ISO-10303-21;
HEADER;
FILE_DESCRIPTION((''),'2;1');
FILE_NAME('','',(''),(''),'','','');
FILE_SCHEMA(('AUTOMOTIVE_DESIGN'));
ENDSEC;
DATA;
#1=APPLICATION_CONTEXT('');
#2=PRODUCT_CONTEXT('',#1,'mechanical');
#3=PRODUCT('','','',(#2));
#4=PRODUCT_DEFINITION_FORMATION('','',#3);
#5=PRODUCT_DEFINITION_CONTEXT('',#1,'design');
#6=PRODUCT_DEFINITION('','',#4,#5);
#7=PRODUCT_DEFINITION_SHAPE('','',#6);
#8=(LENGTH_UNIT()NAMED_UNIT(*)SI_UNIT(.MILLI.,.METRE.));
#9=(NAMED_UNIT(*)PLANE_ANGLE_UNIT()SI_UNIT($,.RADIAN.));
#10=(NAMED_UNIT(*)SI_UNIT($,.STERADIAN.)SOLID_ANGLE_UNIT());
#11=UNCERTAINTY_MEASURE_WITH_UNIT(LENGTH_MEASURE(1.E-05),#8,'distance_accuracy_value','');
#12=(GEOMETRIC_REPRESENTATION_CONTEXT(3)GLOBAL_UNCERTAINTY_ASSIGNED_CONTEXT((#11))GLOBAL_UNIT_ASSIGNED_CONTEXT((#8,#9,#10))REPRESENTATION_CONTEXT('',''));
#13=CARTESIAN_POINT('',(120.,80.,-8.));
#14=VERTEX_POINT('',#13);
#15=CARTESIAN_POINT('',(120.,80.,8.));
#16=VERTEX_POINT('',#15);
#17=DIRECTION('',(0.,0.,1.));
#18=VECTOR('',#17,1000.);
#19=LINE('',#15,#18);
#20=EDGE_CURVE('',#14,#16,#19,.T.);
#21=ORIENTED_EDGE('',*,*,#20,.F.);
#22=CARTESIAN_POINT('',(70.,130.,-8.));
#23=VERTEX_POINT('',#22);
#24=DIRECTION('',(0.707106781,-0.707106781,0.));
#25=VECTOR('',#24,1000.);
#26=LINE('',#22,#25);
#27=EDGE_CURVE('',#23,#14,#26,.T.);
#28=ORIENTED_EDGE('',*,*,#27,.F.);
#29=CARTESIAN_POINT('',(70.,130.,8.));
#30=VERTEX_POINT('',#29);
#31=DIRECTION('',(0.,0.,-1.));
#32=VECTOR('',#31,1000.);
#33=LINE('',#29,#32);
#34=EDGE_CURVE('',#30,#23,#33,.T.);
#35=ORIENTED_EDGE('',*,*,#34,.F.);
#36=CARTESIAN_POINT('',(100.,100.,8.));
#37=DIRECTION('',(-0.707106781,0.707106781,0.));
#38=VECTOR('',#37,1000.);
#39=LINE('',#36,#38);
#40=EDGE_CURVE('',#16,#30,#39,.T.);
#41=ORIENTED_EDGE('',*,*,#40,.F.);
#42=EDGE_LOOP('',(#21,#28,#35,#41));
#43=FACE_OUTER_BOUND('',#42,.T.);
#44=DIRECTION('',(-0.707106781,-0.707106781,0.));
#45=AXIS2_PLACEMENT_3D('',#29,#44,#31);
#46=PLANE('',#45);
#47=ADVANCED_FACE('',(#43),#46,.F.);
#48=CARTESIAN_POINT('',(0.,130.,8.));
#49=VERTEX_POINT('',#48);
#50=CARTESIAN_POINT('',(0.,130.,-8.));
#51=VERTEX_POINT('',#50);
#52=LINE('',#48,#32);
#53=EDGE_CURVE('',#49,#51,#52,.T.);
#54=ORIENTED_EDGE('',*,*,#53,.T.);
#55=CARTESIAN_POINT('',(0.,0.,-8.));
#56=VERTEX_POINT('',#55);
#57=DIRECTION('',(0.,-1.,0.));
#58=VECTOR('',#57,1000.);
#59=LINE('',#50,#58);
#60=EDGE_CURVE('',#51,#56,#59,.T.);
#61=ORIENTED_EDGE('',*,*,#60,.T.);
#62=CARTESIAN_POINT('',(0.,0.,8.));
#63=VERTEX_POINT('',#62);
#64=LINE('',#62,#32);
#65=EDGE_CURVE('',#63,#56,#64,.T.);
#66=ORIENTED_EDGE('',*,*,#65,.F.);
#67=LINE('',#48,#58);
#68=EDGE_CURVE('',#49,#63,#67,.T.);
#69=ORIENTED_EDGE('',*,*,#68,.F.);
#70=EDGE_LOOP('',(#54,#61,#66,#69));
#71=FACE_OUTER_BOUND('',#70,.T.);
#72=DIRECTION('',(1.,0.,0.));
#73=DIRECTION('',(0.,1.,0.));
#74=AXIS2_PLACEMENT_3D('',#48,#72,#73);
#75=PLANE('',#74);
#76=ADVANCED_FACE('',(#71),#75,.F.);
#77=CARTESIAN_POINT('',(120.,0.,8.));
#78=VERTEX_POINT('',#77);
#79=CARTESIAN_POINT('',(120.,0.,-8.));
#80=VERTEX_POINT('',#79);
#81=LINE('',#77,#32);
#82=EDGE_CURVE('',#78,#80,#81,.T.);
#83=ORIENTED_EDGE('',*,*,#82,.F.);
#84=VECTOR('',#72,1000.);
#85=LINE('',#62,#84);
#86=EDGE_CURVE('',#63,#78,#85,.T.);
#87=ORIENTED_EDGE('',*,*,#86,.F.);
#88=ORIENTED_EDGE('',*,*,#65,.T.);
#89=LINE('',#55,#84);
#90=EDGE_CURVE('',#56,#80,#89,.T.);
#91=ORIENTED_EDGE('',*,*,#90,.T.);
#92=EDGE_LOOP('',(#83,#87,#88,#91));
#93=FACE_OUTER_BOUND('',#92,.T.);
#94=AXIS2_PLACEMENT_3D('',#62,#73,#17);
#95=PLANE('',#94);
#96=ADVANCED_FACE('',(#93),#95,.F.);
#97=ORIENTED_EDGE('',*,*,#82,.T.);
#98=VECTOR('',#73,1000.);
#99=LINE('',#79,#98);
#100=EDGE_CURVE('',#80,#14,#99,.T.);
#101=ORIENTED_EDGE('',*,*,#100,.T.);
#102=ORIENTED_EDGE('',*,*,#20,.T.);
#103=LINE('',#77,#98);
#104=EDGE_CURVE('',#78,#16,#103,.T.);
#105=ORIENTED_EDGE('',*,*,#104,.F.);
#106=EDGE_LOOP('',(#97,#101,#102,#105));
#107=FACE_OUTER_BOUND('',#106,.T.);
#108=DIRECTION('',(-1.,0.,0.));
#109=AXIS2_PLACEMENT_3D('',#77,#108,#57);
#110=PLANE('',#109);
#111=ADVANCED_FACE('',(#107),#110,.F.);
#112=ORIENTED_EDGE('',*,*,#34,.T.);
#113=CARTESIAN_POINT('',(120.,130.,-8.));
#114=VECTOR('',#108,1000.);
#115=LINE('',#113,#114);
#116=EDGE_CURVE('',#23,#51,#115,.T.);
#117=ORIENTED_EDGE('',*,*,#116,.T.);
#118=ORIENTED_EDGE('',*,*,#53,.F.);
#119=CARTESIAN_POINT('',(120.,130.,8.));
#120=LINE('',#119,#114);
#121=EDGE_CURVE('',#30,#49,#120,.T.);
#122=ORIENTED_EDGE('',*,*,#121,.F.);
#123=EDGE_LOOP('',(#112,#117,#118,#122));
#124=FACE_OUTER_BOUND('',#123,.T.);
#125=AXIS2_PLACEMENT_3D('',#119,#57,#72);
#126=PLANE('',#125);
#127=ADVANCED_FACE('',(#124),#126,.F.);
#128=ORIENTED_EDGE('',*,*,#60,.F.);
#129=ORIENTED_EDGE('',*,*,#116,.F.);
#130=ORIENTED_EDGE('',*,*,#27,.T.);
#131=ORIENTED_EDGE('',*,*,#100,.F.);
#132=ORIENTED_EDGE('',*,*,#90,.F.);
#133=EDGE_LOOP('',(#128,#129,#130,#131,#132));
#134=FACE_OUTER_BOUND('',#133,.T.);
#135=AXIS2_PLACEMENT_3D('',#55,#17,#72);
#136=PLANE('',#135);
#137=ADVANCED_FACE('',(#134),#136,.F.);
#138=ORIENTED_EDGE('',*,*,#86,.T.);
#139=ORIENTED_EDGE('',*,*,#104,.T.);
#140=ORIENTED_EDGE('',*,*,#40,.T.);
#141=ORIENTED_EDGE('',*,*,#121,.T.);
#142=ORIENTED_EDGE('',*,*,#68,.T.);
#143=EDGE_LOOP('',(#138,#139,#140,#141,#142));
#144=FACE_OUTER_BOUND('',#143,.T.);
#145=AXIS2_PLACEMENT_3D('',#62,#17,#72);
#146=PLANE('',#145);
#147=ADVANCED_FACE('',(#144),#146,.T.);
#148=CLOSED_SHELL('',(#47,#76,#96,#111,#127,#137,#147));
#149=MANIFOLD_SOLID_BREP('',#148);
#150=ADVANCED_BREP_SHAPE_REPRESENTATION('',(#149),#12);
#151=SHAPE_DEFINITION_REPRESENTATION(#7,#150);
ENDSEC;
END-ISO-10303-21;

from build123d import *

# Parameters (mm, degrees)
SKETCH1_W           = 120
SKETCH1_H           = 130
BOSS_EXTRUDE1_DEPTH = 8
CHAMFER1_SIZE       = 50


with BuildPart() as part:
    # Sketch1 → Boss-Extrude1 (new, symmetric)
    with BuildSketch(Plane.XY):
        with Locations((60, 65)):
            Rectangle(SKETCH1_W, SKETCH1_H)
    extrude(amount=BOSS_EXTRUDE1_DEPTH, both=True)

    # Chamfer1
    chamfer1_edges = [part.edges().sort_by_distance(p)[0] for p in [
        (120, 130, 0),
    ]]
    chamfer(chamfer1_edges, length=CHAMFER1_SIZE)


solid = part.part
